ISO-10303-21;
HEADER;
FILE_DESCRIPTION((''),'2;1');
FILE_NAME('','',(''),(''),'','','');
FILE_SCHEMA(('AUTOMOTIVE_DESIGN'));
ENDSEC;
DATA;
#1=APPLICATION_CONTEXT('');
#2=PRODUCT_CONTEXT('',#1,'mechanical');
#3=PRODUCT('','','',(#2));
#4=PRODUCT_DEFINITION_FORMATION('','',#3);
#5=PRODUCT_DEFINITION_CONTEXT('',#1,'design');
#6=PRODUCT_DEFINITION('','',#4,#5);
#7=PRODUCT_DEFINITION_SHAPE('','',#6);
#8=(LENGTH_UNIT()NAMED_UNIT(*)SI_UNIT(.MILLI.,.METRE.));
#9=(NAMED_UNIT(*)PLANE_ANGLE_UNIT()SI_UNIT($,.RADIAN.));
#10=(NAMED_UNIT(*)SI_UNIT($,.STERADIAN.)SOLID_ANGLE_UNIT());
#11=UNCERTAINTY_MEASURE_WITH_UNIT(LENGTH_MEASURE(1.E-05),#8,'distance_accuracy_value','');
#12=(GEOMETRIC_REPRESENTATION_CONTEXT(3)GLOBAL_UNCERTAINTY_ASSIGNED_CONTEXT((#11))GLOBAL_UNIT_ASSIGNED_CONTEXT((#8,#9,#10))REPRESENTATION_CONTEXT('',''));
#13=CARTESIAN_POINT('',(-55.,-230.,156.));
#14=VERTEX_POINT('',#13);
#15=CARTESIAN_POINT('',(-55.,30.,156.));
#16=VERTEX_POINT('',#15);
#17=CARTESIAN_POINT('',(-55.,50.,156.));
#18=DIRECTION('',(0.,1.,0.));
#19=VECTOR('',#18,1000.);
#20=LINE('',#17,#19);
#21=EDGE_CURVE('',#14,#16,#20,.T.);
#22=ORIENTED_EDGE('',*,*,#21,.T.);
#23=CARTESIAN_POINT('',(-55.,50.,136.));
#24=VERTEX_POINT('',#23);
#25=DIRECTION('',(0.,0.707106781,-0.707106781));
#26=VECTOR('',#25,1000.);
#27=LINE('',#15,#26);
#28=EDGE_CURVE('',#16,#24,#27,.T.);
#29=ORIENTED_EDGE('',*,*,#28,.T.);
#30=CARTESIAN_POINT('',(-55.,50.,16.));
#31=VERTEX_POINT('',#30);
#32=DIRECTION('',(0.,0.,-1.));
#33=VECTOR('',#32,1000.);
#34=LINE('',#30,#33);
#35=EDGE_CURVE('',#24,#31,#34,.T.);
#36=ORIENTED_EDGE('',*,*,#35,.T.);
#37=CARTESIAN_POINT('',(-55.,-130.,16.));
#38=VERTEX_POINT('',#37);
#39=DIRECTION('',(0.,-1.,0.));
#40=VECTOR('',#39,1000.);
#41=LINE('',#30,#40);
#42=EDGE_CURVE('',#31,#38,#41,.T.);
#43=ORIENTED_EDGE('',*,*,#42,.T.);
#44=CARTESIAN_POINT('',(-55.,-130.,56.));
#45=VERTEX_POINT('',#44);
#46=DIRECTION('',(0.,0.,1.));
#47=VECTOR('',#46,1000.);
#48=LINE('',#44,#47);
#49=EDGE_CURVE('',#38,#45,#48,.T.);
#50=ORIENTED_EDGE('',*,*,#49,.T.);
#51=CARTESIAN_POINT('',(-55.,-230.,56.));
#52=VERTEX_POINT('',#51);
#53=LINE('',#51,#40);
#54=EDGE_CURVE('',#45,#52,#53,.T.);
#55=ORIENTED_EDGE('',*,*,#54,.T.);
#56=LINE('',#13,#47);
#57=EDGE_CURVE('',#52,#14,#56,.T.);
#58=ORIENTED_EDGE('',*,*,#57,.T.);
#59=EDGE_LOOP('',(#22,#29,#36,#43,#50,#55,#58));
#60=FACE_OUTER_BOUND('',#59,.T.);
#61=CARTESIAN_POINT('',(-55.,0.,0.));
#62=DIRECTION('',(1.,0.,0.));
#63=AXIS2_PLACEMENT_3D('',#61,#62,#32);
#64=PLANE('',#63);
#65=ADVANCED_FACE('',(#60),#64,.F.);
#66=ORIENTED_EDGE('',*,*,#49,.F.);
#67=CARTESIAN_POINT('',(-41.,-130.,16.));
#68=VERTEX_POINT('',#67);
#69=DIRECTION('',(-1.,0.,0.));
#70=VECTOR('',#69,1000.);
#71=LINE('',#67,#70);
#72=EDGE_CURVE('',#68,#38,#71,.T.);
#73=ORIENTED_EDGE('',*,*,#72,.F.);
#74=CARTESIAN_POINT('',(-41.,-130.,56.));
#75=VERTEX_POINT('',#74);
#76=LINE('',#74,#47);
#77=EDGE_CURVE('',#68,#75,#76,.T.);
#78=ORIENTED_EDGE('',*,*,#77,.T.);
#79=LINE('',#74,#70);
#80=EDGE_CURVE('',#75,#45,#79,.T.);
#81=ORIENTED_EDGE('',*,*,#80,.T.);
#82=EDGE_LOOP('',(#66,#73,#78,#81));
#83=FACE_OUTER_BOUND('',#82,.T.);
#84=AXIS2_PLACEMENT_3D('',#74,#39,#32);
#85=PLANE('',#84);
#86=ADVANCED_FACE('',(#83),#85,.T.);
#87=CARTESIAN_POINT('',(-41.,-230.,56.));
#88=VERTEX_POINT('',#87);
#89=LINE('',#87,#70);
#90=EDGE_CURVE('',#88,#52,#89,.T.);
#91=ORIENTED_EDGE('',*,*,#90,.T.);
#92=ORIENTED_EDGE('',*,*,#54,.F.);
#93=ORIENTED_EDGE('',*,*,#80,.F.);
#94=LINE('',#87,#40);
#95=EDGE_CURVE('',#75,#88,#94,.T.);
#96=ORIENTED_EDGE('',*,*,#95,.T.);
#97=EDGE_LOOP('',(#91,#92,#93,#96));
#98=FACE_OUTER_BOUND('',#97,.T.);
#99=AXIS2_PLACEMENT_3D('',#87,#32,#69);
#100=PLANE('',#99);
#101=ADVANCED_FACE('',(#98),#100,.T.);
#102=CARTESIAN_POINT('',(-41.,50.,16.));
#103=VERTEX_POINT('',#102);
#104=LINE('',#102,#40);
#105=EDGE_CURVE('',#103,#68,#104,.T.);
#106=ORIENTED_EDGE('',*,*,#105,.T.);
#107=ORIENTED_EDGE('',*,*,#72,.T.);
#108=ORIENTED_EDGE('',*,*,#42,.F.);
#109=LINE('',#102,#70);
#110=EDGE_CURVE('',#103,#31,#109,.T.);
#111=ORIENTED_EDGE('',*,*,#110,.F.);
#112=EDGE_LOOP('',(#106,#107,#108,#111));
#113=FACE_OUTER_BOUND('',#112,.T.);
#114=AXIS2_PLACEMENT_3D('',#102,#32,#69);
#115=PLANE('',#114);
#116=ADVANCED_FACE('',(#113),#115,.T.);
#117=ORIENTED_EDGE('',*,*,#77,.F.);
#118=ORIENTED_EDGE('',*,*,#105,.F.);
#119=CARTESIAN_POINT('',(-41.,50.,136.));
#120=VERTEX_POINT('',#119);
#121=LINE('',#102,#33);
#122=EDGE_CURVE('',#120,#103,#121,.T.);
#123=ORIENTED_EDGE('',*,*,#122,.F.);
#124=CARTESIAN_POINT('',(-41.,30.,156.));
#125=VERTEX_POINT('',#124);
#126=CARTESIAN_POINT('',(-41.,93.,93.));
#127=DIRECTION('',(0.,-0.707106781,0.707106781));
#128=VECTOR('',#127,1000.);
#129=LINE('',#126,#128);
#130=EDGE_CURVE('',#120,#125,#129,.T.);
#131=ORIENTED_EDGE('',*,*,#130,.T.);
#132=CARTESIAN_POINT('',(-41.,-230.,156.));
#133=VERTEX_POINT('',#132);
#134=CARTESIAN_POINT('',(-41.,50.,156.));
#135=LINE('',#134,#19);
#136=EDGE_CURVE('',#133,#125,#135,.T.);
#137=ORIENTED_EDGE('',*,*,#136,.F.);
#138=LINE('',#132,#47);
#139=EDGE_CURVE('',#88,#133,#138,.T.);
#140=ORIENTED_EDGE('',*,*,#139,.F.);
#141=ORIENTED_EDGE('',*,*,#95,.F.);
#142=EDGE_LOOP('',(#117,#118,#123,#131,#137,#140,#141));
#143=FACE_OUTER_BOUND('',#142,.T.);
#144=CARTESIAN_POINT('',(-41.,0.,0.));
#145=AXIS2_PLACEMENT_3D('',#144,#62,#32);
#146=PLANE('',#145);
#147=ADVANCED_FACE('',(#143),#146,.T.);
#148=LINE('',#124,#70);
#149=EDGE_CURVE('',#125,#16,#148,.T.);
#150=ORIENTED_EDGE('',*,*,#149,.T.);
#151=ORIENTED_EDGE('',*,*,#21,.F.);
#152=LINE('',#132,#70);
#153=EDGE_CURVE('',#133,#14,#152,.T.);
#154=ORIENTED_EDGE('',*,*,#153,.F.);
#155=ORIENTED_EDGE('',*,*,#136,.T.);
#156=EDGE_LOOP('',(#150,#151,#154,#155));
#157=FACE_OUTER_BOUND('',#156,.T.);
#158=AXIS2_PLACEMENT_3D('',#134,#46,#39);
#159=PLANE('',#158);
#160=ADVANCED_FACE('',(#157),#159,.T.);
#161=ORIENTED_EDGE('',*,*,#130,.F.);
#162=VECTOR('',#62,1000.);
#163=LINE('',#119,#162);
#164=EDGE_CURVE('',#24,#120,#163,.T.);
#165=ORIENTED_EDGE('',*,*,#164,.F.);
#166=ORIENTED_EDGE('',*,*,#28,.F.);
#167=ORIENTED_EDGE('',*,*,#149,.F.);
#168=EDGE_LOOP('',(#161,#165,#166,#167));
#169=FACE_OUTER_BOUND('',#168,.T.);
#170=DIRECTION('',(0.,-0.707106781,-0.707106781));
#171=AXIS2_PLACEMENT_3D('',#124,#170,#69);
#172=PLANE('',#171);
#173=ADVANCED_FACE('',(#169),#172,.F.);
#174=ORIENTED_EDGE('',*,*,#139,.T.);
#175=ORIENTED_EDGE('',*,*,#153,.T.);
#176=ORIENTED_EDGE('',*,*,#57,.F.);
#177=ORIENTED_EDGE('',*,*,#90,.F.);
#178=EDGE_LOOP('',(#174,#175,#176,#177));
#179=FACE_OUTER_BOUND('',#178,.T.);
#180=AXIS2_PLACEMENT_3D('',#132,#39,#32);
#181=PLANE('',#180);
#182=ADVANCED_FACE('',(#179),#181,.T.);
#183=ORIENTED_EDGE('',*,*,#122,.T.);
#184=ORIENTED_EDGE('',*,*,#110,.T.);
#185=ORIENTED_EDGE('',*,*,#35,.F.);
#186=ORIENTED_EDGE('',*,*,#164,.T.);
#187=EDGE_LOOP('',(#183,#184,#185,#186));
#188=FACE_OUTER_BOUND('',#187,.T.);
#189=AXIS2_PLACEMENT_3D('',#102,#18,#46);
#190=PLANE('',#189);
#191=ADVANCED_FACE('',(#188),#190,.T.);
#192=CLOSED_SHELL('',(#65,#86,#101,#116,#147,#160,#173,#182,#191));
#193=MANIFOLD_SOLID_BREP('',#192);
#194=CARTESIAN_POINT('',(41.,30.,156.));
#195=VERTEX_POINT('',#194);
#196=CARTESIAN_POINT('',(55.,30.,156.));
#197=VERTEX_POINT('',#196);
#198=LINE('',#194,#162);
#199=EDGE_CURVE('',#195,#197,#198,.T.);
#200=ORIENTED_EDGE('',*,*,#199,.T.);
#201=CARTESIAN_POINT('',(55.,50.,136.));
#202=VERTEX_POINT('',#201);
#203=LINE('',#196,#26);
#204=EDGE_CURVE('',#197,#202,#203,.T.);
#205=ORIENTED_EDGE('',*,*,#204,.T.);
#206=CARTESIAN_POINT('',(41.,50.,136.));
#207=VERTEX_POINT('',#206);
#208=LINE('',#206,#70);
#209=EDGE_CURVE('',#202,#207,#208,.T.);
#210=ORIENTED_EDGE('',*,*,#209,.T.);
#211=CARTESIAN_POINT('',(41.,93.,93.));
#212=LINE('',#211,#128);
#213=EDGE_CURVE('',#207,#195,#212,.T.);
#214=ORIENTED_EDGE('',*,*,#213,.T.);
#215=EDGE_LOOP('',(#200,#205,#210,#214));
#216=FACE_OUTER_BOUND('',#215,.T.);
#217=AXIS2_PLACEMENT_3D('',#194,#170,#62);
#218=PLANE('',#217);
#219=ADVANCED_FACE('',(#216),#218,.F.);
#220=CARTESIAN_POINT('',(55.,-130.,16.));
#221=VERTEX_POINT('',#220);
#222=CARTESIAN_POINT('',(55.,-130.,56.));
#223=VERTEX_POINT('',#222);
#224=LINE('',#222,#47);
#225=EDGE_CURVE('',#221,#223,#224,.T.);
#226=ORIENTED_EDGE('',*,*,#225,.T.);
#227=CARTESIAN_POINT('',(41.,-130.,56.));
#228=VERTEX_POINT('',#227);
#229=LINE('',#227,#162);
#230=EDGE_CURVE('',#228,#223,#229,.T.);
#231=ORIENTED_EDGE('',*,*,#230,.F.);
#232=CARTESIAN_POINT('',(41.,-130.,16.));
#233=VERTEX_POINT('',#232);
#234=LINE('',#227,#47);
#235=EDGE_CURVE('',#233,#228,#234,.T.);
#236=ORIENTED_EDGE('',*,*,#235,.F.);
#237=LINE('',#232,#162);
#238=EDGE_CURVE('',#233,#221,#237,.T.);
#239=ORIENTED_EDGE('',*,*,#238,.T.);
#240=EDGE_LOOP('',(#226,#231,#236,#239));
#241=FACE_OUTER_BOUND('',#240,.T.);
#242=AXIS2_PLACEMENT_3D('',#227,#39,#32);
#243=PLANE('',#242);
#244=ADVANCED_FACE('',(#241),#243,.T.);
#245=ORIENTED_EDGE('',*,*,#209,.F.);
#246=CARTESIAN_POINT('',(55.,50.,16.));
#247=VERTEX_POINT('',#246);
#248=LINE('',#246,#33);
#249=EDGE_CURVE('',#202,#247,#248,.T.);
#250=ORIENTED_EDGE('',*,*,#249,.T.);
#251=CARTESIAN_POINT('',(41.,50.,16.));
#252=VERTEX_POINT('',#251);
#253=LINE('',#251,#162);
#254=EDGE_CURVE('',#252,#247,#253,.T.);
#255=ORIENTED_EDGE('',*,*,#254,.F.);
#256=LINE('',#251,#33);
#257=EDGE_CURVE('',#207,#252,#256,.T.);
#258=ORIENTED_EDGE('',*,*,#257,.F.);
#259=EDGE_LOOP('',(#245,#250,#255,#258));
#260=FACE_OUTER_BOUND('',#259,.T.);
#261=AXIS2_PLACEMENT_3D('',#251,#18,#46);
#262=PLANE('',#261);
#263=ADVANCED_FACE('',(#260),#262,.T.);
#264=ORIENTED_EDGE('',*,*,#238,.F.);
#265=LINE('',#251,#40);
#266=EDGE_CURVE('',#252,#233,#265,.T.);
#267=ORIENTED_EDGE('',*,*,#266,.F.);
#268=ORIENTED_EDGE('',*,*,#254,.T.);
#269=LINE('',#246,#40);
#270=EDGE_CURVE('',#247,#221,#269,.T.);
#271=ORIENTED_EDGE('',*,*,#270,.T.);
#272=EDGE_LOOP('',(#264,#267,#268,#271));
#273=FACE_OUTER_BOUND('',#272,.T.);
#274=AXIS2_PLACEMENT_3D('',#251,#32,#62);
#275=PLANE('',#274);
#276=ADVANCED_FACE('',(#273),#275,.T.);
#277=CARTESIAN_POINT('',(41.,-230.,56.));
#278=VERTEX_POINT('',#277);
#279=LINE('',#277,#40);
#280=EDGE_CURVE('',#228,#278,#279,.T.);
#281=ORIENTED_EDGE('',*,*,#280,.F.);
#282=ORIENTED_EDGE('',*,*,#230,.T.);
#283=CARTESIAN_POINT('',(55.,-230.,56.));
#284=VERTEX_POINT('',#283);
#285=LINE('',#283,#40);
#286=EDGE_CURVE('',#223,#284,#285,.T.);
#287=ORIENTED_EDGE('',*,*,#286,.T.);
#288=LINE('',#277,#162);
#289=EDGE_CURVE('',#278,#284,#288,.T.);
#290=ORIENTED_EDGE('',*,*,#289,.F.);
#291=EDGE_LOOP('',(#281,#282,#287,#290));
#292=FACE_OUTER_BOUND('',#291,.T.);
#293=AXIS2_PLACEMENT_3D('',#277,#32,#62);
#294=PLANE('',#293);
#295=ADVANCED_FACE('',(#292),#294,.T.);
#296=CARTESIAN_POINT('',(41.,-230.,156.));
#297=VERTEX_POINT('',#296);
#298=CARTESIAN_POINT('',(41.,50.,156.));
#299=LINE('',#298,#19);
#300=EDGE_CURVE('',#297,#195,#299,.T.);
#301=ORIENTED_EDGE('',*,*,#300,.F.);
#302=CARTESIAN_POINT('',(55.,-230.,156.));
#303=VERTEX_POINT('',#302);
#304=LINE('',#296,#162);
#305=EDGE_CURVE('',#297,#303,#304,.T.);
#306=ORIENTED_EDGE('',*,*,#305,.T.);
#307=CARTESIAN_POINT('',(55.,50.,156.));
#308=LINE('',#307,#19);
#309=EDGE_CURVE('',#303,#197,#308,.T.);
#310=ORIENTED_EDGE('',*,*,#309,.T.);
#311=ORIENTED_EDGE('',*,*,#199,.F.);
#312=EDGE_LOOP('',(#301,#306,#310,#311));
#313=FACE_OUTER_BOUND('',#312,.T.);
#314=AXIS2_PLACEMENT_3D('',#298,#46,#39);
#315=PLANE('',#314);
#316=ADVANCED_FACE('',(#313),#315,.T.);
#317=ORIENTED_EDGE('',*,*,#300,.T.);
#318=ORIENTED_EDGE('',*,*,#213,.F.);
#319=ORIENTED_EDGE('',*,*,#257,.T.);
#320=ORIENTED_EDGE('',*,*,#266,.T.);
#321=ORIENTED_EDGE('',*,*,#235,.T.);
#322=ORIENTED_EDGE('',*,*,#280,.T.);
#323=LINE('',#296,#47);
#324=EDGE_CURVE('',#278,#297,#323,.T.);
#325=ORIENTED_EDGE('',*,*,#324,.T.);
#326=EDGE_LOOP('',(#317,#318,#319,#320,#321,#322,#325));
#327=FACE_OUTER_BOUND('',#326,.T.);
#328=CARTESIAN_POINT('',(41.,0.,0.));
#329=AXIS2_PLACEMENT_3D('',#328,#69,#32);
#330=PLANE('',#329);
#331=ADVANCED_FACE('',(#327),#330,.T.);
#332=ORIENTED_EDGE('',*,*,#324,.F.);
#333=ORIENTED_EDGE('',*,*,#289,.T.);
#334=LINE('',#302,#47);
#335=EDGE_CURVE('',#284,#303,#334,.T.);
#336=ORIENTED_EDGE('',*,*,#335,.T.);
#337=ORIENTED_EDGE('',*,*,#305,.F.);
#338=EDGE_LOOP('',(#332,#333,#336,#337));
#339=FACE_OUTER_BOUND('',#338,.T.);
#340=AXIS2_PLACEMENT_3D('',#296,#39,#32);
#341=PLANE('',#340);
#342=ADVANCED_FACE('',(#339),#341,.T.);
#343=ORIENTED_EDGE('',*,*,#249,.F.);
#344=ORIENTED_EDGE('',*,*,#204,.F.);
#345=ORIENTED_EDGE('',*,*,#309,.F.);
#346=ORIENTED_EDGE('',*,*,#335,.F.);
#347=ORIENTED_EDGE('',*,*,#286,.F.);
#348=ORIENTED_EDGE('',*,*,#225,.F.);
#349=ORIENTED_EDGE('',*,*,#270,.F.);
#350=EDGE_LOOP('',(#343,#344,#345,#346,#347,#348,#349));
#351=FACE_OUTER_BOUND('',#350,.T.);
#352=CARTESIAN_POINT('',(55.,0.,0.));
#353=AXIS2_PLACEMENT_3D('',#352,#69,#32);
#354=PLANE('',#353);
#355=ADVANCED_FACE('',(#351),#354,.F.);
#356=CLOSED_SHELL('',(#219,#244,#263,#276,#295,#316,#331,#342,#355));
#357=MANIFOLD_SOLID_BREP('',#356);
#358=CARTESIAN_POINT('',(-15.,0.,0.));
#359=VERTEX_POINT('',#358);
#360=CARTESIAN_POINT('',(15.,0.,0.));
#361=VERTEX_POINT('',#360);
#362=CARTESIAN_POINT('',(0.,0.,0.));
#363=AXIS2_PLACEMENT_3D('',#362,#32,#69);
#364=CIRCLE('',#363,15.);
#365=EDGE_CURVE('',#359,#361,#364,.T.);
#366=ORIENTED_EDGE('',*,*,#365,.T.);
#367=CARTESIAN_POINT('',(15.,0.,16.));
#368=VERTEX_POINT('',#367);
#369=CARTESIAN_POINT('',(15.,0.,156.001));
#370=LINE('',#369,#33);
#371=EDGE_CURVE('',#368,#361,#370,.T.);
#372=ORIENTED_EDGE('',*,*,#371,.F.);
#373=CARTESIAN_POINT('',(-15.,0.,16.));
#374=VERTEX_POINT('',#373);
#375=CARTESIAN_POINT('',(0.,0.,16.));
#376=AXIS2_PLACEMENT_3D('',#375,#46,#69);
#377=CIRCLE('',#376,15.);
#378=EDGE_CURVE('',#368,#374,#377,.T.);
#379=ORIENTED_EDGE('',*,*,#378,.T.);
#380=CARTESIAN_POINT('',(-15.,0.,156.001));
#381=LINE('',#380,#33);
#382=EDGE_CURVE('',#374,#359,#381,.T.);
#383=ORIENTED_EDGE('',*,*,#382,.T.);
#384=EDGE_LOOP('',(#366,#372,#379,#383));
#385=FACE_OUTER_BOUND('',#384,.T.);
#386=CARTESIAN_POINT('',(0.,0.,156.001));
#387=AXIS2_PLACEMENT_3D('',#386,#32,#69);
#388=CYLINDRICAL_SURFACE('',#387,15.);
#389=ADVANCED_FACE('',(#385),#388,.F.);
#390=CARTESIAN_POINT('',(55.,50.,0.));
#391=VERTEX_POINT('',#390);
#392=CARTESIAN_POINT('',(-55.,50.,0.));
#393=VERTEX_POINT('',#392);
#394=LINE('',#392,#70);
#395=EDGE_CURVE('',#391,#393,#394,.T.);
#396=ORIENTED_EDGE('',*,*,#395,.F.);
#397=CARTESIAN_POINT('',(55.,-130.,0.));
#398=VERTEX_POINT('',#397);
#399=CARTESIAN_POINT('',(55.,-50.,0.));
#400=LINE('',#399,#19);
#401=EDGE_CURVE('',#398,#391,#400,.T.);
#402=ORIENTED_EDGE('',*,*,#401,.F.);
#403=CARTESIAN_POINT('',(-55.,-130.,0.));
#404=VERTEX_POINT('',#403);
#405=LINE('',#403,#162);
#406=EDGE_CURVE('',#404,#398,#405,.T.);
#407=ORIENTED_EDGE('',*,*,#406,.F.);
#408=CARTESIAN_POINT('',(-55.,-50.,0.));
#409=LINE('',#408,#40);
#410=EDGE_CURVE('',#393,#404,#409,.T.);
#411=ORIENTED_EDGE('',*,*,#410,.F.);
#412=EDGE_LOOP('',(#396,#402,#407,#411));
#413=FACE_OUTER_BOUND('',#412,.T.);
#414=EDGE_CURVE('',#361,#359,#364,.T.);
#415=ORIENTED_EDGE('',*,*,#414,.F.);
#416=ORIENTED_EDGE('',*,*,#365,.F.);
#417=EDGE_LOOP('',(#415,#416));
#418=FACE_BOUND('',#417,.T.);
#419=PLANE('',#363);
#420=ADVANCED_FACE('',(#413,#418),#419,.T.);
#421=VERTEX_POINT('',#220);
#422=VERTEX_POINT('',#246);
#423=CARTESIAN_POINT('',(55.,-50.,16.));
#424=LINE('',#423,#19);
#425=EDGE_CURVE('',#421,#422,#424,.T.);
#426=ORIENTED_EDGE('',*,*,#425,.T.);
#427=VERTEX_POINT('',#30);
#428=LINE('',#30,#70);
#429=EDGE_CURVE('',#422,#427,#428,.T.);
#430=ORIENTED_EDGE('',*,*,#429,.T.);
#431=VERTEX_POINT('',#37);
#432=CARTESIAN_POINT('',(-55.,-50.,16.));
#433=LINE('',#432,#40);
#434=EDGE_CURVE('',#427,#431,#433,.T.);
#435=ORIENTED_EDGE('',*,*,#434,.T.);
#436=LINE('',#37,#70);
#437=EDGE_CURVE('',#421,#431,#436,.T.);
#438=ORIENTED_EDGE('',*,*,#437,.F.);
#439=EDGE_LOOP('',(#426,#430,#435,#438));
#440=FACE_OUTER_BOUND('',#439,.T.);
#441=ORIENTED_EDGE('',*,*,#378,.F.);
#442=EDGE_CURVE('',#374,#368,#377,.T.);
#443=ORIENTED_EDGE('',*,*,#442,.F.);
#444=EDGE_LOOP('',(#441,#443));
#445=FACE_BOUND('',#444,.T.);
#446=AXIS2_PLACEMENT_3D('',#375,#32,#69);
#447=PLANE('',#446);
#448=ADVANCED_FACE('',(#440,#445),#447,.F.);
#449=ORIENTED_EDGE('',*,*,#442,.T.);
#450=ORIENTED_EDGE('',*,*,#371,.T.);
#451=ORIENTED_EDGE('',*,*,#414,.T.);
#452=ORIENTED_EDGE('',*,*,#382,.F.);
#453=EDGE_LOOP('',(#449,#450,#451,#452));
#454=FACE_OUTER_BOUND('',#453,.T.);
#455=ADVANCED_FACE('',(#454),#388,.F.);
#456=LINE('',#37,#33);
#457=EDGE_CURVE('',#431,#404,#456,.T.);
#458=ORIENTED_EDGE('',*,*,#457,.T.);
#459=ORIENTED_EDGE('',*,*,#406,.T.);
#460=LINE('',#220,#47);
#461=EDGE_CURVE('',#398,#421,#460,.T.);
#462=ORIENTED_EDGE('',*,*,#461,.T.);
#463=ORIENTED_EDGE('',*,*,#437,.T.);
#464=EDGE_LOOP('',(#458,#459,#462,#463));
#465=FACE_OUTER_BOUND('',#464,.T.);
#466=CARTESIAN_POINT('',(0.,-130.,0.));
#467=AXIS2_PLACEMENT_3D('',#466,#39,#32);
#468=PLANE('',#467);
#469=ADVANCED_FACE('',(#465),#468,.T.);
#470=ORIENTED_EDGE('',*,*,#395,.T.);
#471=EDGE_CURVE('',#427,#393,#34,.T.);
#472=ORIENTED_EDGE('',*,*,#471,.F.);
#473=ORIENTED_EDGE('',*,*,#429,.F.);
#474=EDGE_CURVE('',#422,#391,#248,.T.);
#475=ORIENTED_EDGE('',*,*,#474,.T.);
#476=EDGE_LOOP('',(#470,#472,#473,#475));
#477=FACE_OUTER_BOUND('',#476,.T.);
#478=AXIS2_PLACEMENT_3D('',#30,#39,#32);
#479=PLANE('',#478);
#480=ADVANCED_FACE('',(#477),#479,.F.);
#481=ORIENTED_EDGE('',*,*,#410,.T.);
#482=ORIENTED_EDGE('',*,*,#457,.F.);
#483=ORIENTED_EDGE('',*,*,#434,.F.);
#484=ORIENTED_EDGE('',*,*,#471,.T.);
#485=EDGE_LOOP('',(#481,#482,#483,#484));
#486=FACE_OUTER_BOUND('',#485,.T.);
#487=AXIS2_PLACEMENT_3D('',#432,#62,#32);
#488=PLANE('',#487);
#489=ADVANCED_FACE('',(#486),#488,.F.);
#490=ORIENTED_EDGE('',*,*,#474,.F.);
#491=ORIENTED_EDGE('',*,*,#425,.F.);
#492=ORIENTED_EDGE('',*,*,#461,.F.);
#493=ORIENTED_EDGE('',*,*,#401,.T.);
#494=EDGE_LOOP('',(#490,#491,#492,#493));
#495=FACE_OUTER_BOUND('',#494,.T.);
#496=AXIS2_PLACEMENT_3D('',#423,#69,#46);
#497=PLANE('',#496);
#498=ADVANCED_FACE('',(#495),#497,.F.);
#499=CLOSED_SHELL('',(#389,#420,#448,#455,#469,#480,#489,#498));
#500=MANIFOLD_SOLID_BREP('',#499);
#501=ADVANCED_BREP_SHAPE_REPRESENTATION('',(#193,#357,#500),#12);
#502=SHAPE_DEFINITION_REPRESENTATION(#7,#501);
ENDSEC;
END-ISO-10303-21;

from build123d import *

# Parameters (mm, degrees)
SKETCH_1_W          = 110
SKETCH_1_H          = 100
EXTRUDE_1_DEPTH     = 16
EXTRUDE_2_DEPTH     = 14
CHAMFER_1_SIZE      = 20
SKETCH_3_R          = 15
CUT_EXTRUDE_1_DEPTH = 16
SKETCH_4_W          = 110
SKETCH_4_H          = 16
EXTRUDE_3_DEPTH     = 80


with BuildPart() as part:
    # 草图1 → 凸台-拉伸1 (new body)
    with BuildSketch(Plane.XY):
        Rectangle(SKETCH_1_W, SKETCH_1_H)
    extrude(amount=EXTRUDE_1_DEPTH)

    # 草图3 → 切除-拉伸1 (cut)
    with BuildSketch(Plane(origin=(0, 0, 0), x_dir=(-1, 0, 0), z_dir=(0, 0, -1))):
        Circle(SKETCH_3_R)
    extrude(amount=-CUT_EXTRUDE_1_DEPTH, mode=Mode.SUBTRACT)

    # 草图4 → 凸台-拉伸3 (add)
    with BuildSketch(Plane.XZ.offset(50)):
        with Locations((0, 8)):
            Rectangle(SKETCH_4_W, SKETCH_4_H)
    extrude(amount=EXTRUDE_3_DEPTH)


with BuildPart() as body_2:
    # 草图2 → 凸台-拉伸2 (new body)
    with BuildSketch(Plane.ZY.offset(55)):
        Polygon((16, 50), (16, -130), (56, -130), (56, -230), (156, -230), (156, 50), align=None)
    extrude(amount=-EXTRUDE_2_DEPTH)

    # 倒角1
    chamfer_1_edges = [body_2.edges().sort_by_distance(p)[0] for p in [
        (-48, 50, 156),
    ]]
    chamfer(chamfer_1_edges, length=CHAMFER_1_SIZE)


with BuildPart() as body_3:
    # 镜向1: mirrored copy
    add(body_2.part.mirror(Plane(origin=(0, 0, 0), x_dir=(0, 0, 1), z_dir=(1, 0, 0))))


solid = Compound([part.part, body_2.part, body_3.part])
